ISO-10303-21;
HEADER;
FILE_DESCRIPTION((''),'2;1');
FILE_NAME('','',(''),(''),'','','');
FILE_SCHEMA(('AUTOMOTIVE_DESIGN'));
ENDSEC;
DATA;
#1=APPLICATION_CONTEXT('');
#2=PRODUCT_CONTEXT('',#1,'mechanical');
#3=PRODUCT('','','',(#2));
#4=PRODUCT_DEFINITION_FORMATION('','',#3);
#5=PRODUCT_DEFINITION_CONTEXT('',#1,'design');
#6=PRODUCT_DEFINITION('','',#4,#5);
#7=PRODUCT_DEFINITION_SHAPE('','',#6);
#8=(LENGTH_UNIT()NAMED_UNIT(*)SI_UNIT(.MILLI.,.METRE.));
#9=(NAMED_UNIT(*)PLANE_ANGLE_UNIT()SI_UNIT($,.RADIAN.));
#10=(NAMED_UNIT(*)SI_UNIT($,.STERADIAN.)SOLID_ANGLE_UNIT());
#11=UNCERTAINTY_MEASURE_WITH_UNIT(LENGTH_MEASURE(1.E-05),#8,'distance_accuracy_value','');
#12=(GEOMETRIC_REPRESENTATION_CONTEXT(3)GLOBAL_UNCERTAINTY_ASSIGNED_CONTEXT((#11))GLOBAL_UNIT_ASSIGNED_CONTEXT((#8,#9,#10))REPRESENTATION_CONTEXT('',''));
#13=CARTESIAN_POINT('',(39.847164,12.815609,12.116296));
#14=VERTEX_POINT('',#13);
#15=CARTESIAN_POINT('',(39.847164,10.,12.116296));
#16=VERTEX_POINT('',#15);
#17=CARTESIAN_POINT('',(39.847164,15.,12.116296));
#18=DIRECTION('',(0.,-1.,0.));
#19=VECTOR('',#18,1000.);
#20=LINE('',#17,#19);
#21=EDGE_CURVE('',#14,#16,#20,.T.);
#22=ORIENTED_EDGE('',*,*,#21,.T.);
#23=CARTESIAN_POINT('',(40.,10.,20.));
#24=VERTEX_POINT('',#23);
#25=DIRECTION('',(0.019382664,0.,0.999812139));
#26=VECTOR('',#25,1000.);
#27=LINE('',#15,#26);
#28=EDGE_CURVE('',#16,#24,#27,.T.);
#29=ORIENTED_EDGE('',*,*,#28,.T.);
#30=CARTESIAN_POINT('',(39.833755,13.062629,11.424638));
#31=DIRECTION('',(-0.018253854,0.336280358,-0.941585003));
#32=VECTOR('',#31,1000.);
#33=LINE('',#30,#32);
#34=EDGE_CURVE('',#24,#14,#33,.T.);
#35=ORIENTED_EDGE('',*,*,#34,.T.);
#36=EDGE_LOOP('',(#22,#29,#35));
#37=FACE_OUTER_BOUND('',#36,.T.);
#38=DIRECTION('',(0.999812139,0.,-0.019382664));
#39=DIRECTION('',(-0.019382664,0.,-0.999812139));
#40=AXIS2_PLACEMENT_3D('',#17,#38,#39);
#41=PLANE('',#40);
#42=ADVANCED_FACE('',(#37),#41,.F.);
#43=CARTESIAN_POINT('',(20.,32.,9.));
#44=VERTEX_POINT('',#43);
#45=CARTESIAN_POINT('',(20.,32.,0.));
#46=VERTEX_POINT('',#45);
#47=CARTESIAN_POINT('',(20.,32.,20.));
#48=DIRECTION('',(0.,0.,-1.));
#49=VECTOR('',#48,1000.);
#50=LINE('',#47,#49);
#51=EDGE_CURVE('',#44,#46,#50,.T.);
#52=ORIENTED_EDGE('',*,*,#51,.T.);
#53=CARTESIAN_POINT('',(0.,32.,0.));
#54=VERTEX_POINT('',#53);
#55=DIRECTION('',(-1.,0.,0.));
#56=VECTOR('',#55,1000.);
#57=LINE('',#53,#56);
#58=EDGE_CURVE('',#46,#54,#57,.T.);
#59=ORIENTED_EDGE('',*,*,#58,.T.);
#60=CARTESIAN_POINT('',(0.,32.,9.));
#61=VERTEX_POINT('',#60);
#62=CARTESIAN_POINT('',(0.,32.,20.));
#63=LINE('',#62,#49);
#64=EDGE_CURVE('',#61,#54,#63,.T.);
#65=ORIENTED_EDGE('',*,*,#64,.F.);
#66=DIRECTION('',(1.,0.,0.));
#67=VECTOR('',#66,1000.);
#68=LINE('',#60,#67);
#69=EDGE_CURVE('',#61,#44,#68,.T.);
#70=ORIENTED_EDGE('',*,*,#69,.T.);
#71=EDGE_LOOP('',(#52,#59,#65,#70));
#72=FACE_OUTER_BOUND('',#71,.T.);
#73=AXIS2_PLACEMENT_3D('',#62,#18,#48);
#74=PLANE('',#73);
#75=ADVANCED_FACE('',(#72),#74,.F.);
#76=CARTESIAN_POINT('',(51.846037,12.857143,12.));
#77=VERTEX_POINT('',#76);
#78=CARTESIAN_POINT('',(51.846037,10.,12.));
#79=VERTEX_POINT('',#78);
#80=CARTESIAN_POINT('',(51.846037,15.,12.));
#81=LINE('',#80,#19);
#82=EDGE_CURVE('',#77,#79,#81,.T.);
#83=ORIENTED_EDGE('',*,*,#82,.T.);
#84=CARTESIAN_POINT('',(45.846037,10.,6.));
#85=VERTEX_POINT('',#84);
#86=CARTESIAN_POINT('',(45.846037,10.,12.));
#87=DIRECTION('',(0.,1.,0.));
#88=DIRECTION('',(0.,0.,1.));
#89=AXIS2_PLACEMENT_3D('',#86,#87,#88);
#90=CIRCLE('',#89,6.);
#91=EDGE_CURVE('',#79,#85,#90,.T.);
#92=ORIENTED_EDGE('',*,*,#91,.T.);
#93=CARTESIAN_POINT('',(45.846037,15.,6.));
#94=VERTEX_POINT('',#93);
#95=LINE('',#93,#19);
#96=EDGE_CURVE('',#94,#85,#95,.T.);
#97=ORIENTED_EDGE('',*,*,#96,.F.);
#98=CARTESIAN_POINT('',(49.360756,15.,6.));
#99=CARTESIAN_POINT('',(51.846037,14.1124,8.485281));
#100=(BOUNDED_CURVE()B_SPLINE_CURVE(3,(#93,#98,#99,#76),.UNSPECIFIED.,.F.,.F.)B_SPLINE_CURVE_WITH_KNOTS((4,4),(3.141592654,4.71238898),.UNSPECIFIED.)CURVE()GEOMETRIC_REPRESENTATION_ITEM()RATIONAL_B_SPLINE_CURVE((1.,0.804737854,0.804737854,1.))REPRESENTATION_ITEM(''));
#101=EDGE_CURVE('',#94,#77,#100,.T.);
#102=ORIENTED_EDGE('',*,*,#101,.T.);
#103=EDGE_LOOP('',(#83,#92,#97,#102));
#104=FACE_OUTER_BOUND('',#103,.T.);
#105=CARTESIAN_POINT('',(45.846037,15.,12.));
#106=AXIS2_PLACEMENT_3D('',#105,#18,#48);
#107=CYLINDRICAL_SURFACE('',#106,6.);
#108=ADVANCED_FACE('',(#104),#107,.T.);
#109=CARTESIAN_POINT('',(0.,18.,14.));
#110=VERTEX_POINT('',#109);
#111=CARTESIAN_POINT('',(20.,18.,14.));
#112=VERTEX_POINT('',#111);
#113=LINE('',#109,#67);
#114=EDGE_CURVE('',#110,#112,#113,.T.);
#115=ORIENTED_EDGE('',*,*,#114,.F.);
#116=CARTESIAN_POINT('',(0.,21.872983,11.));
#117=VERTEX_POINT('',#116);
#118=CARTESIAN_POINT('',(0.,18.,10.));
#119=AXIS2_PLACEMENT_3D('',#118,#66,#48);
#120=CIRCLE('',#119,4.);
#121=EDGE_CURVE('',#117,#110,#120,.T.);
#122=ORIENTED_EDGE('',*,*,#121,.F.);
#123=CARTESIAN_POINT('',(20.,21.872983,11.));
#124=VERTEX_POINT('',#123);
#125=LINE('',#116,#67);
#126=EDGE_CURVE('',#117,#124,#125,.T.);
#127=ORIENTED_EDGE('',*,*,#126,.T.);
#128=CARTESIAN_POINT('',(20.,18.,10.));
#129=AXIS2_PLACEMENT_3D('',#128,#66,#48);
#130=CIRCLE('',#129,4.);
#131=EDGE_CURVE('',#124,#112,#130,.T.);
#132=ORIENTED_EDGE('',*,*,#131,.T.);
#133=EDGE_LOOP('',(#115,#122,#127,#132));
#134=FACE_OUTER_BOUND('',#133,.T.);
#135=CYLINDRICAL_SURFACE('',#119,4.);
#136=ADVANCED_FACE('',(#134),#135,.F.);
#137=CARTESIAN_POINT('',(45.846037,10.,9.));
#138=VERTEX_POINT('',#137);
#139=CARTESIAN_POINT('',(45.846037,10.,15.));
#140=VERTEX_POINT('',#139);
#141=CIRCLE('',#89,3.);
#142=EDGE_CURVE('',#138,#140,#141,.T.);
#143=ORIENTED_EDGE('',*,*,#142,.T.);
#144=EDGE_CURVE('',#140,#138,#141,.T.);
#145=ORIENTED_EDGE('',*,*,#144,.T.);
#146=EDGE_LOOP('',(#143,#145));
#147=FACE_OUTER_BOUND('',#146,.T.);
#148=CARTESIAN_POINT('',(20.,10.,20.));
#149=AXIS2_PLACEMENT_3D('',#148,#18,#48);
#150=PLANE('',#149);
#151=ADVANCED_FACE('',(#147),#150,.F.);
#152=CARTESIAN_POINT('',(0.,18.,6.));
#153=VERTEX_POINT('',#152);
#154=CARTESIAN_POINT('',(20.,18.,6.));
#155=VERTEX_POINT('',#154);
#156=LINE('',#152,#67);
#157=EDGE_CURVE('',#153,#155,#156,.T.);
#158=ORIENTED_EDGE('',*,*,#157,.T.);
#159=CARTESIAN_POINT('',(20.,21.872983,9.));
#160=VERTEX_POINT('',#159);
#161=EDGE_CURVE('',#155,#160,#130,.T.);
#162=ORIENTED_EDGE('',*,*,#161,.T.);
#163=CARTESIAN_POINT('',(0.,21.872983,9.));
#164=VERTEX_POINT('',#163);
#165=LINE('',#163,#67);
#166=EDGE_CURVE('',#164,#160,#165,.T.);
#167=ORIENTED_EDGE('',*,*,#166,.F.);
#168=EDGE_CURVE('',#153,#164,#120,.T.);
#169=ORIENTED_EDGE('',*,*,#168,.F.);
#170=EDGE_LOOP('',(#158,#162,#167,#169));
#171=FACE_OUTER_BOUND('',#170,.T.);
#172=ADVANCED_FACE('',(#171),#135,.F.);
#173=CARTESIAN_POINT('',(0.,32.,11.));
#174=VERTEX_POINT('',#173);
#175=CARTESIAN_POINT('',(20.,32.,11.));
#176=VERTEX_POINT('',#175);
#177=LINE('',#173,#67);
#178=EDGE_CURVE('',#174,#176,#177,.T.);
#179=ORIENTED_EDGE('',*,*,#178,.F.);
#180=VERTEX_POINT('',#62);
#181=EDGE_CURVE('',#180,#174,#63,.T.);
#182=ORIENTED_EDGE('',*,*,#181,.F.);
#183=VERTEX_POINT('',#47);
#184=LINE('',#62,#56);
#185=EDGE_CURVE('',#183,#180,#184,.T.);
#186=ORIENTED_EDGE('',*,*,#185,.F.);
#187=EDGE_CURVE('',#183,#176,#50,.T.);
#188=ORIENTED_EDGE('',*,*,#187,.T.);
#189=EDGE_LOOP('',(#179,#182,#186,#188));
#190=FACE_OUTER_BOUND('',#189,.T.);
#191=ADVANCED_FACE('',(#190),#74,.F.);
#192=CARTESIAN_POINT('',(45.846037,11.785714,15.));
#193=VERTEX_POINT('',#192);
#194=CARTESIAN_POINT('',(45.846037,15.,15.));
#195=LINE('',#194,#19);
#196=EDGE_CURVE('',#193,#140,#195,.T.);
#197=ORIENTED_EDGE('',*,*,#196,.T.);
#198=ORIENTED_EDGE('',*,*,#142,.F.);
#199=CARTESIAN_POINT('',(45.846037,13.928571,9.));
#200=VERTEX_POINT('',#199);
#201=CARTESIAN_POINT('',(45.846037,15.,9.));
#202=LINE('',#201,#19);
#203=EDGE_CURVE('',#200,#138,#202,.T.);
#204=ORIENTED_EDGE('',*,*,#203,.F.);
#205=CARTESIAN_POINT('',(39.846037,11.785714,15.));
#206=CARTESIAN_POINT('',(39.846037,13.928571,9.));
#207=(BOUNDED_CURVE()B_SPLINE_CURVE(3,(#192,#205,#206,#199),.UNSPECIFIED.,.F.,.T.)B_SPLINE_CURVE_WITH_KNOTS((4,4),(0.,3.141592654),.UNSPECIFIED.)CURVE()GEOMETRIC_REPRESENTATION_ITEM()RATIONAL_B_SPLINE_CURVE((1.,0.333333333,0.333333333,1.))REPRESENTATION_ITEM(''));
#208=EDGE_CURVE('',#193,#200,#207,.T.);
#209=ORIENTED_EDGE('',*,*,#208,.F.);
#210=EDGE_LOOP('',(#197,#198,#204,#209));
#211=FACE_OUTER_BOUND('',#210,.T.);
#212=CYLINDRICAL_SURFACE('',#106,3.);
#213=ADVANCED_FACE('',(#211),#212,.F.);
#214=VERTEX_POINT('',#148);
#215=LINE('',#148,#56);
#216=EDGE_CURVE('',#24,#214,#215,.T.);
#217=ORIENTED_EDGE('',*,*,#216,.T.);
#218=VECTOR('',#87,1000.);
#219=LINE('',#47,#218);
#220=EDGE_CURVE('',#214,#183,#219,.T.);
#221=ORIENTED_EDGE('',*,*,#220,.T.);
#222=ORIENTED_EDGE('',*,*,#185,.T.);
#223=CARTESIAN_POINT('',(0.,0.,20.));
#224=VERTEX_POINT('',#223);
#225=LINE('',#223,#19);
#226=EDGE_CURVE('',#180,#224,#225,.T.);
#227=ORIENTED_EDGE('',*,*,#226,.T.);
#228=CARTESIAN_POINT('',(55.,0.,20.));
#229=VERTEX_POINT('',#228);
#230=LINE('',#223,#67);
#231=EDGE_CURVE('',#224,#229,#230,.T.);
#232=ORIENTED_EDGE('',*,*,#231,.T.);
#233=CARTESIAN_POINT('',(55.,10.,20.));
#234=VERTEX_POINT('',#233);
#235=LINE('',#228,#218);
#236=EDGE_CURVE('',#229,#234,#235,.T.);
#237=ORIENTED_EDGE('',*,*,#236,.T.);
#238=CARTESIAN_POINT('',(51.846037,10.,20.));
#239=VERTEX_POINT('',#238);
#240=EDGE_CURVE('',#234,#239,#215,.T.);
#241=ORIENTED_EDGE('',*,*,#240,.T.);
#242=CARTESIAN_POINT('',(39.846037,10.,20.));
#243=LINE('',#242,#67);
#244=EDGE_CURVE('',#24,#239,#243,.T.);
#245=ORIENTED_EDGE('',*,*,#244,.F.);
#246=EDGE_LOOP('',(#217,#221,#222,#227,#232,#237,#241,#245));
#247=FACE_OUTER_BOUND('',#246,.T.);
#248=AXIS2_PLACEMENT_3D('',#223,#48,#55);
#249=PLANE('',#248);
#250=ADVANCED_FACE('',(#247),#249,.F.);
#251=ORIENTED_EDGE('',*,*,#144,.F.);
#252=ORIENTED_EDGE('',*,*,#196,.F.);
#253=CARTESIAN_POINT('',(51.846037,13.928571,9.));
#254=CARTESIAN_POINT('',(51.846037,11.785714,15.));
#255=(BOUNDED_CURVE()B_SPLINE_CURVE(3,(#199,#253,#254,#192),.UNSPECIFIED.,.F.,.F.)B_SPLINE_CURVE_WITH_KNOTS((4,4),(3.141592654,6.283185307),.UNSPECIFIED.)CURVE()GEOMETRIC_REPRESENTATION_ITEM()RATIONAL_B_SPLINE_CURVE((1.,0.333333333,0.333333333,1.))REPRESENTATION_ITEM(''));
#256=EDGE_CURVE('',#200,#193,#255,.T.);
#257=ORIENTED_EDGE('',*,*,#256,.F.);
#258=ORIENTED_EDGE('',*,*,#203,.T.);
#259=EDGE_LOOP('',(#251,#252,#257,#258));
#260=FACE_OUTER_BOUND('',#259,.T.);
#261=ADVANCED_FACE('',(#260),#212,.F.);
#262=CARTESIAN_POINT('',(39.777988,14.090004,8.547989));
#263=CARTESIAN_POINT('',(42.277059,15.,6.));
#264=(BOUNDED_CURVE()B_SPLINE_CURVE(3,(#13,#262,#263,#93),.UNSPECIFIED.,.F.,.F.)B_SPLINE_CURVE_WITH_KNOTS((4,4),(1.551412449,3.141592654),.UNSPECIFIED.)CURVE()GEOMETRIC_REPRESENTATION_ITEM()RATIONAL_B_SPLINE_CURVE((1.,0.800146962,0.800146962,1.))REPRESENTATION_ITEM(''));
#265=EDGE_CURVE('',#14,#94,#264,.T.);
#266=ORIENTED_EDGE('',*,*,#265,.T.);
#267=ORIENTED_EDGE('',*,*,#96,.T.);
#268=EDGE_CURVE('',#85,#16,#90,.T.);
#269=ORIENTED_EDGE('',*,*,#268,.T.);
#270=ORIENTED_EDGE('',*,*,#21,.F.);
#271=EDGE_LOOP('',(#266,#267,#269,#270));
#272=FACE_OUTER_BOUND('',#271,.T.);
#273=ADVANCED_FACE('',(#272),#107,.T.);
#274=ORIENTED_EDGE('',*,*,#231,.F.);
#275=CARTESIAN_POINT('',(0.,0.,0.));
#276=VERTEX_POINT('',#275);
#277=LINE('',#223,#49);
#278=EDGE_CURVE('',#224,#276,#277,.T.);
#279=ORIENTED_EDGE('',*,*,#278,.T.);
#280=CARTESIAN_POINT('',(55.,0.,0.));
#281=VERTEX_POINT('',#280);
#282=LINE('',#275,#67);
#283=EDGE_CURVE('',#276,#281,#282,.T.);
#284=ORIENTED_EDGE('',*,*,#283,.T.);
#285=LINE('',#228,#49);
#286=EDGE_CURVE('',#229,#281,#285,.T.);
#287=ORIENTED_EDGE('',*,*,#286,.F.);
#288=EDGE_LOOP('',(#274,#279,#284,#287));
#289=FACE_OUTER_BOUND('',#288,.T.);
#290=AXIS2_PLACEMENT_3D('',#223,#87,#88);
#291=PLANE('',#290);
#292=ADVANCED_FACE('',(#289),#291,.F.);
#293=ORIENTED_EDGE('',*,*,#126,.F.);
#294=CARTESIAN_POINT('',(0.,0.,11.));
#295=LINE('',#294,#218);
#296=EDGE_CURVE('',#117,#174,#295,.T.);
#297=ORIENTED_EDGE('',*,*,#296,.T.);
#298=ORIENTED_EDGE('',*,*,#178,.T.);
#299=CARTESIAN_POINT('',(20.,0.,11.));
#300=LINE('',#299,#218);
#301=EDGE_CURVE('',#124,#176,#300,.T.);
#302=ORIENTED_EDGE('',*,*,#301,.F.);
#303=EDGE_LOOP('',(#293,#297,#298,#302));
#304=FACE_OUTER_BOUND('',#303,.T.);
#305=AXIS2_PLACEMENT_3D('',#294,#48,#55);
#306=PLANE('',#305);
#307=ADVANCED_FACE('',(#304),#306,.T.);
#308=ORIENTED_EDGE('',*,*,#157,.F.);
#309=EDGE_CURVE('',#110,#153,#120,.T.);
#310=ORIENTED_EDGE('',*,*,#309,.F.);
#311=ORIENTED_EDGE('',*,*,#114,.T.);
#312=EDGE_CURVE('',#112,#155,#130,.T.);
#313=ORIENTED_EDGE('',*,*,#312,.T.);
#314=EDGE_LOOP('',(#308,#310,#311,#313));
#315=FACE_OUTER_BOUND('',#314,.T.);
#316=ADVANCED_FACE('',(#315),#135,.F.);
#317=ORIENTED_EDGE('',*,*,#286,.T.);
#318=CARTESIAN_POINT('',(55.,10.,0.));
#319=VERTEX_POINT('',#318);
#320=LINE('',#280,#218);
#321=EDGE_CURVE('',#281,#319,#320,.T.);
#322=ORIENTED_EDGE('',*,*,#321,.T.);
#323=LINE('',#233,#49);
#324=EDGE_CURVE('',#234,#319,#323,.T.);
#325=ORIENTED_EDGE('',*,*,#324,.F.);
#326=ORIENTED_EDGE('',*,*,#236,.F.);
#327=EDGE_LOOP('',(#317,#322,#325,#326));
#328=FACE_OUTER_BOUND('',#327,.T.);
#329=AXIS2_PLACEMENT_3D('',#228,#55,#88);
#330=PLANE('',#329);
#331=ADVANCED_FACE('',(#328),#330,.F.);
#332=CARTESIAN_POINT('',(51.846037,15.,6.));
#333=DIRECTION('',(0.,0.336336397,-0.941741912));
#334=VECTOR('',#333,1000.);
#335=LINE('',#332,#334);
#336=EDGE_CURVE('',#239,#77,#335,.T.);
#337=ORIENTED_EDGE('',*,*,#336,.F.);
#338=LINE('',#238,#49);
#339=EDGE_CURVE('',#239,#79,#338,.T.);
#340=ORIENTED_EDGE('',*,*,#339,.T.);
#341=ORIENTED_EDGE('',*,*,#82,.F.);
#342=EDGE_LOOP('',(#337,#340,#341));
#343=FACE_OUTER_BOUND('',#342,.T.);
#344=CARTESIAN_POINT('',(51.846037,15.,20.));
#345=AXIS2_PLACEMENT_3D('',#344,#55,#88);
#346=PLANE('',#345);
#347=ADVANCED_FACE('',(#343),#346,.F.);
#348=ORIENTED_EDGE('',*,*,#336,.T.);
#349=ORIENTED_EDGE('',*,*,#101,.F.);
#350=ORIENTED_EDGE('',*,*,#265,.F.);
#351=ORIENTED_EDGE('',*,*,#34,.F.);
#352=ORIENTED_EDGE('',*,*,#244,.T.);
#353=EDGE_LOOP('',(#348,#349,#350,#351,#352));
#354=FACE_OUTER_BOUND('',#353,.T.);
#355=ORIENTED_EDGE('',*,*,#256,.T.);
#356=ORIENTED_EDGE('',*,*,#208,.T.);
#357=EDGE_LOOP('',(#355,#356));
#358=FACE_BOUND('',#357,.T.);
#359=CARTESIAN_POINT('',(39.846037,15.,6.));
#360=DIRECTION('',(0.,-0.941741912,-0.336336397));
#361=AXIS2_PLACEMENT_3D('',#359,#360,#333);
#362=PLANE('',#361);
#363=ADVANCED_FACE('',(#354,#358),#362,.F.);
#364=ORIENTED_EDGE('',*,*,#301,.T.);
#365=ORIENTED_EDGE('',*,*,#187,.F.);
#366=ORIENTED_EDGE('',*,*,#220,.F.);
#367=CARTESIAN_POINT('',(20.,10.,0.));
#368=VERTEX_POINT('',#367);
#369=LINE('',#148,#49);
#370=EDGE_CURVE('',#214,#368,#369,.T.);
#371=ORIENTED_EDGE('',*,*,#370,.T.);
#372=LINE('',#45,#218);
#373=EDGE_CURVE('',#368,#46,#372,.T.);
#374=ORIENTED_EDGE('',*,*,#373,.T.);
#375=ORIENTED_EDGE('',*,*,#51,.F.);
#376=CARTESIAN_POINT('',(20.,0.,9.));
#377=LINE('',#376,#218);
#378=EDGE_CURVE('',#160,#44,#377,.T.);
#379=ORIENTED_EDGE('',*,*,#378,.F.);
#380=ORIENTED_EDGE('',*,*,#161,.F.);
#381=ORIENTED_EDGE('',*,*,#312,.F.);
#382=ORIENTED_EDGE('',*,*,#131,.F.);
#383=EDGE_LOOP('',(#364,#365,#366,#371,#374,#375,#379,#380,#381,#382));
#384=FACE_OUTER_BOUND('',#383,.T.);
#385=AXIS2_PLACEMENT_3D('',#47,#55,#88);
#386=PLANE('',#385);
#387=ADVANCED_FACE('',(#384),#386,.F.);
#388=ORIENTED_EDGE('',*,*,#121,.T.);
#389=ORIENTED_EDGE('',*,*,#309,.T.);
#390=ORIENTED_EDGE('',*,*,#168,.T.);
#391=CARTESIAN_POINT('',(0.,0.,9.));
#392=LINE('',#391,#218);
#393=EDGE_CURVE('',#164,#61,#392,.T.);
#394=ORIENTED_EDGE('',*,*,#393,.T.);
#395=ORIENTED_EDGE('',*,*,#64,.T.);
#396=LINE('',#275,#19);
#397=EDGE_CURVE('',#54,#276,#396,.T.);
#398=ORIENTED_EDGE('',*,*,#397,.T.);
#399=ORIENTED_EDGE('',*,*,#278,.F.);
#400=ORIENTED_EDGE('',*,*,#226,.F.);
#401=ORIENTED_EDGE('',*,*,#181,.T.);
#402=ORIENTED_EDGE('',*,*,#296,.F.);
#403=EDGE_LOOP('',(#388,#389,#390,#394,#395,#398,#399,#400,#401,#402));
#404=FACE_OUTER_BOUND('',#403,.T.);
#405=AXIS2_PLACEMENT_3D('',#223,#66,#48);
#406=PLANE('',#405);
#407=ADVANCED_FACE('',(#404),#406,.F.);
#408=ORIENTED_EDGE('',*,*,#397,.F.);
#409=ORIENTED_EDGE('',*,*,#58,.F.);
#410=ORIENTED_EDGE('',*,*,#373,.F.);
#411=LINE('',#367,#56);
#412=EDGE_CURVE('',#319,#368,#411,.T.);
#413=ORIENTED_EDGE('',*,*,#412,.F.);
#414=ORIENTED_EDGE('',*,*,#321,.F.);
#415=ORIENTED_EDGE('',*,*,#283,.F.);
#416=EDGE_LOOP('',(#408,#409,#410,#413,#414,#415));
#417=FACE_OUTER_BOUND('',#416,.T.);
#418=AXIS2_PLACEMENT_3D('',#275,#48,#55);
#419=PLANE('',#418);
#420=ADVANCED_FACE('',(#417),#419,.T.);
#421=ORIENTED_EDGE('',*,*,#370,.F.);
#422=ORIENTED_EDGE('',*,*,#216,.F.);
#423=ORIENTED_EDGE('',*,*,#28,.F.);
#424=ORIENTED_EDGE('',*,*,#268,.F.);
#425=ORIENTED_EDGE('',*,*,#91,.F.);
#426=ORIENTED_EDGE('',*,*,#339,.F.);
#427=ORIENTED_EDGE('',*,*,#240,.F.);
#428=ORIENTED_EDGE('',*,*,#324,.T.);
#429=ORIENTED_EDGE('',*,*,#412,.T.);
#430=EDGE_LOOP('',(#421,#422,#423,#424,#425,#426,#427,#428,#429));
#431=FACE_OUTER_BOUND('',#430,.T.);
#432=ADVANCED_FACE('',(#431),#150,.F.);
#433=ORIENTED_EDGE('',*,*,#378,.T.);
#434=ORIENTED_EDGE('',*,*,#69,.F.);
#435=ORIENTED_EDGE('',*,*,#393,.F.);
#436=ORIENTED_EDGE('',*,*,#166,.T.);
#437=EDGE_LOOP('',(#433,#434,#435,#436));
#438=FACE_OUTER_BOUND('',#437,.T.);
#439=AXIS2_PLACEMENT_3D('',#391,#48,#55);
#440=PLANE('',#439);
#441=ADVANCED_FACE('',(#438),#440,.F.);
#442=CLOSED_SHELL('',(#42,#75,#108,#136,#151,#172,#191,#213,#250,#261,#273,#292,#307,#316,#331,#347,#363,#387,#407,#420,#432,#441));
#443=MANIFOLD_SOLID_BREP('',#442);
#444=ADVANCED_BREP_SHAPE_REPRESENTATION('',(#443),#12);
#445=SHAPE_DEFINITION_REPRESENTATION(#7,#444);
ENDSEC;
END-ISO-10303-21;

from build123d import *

# Parameters (mm, degrees)
L_BRACKET_BODY_DEPTH = 20
CLAMP_BORE_SKETCH_R  = 4
CLAMP_BORE_DEPTH     = 52.46843693
CLAMP_SLIT_DEPTH     = 52.46843693
CLEVIS_LUG_SKETCH_R  = 3
CLEVIS_LUG_DEPTH     = 5
LUG_PIN_HOLE_DEPTH   = 12


with BuildPart() as part:
    # Bracket Profile Sketch → L-Bracket Body (new body)
    with BuildSketch(Plane.XY):
        Polygon((0, 0), (55, 0), (55, 10), (20, 10), (20, 32), (0, 32), align=None)
    extrude(amount=L_BRACKET_BODY_DEPTH)

    # Clamp Bore Sketch → Clamp Bore (cut, through all)
    with BuildSketch(Plane(origin=(20, 0, 0), x_dir=(0, 0, -1), z_dir=(1, 0, 0))):
        with Locations((-10, 18)):
            Circle(CLAMP_BORE_SKETCH_R)
    extrude(amount=-CLAMP_BORE_DEPTH, mode=Mode.SUBTRACT)

    # Clamp Slit Sketch → Clamp Slit (cut, through all)
    with BuildSketch(Plane(origin=(20, 0, 0), x_dir=(0, 0, -1), z_dir=(1, 0, 0))):
        with BuildLine():
            ThreePointArc((-11, 21.872983346), (-10, 22), (-9, 21.872983346))
            Line((-9, 21.872983346), (-9, 32))
            Line((-9, 32), (-11, 32))
            Line((-11, 32), (-11, 21.872983346))
        make_face()
    extrude(amount=-CLAMP_SLIT_DEPTH, mode=Mode.SUBTRACT)

    # Clevis Lug Sketch → Clevis Lug (add)
    with BuildSketch(Plane(origin=(0, 10, 0), x_dir=(1, 0, 0), z_dir=(0, 1, 0))):
        with BuildLine():
            Line((39.847164106, -12.116295981), (40, -20))
            Line((40, -20), (51.846036937, -20))
            Line((51.846036937, -20), (51.846036937, -12))
            ThreePointArc((51.846036937, -12), (45.787886215, -6.000281799), (39.847164106, -12.116295981))
        make_face()
        with Locations(Location((45.846036937, -12, 0), (0, 0, 270))):
            Circle(CLEVIS_LUG_SKETCH_R, mode=Mode.SUBTRACT)
    extrude(amount=CLEVIS_LUG_DEPTH)

    # Lug Pin Hole Sketch → Lug Pin Hole (cut)
    with BuildSketch(Plane(origin=(51.846036937, 0, 0), x_dir=(0, 0, -1), z_dir=(1, 0, 0))):
        Polygon((-20, 15), (-20, 10), (-6, 15), align=None)
    extrude(amount=-LUG_PIN_HOLE_DEPTH, mode=Mode.SUBTRACT)


solid = part.part
